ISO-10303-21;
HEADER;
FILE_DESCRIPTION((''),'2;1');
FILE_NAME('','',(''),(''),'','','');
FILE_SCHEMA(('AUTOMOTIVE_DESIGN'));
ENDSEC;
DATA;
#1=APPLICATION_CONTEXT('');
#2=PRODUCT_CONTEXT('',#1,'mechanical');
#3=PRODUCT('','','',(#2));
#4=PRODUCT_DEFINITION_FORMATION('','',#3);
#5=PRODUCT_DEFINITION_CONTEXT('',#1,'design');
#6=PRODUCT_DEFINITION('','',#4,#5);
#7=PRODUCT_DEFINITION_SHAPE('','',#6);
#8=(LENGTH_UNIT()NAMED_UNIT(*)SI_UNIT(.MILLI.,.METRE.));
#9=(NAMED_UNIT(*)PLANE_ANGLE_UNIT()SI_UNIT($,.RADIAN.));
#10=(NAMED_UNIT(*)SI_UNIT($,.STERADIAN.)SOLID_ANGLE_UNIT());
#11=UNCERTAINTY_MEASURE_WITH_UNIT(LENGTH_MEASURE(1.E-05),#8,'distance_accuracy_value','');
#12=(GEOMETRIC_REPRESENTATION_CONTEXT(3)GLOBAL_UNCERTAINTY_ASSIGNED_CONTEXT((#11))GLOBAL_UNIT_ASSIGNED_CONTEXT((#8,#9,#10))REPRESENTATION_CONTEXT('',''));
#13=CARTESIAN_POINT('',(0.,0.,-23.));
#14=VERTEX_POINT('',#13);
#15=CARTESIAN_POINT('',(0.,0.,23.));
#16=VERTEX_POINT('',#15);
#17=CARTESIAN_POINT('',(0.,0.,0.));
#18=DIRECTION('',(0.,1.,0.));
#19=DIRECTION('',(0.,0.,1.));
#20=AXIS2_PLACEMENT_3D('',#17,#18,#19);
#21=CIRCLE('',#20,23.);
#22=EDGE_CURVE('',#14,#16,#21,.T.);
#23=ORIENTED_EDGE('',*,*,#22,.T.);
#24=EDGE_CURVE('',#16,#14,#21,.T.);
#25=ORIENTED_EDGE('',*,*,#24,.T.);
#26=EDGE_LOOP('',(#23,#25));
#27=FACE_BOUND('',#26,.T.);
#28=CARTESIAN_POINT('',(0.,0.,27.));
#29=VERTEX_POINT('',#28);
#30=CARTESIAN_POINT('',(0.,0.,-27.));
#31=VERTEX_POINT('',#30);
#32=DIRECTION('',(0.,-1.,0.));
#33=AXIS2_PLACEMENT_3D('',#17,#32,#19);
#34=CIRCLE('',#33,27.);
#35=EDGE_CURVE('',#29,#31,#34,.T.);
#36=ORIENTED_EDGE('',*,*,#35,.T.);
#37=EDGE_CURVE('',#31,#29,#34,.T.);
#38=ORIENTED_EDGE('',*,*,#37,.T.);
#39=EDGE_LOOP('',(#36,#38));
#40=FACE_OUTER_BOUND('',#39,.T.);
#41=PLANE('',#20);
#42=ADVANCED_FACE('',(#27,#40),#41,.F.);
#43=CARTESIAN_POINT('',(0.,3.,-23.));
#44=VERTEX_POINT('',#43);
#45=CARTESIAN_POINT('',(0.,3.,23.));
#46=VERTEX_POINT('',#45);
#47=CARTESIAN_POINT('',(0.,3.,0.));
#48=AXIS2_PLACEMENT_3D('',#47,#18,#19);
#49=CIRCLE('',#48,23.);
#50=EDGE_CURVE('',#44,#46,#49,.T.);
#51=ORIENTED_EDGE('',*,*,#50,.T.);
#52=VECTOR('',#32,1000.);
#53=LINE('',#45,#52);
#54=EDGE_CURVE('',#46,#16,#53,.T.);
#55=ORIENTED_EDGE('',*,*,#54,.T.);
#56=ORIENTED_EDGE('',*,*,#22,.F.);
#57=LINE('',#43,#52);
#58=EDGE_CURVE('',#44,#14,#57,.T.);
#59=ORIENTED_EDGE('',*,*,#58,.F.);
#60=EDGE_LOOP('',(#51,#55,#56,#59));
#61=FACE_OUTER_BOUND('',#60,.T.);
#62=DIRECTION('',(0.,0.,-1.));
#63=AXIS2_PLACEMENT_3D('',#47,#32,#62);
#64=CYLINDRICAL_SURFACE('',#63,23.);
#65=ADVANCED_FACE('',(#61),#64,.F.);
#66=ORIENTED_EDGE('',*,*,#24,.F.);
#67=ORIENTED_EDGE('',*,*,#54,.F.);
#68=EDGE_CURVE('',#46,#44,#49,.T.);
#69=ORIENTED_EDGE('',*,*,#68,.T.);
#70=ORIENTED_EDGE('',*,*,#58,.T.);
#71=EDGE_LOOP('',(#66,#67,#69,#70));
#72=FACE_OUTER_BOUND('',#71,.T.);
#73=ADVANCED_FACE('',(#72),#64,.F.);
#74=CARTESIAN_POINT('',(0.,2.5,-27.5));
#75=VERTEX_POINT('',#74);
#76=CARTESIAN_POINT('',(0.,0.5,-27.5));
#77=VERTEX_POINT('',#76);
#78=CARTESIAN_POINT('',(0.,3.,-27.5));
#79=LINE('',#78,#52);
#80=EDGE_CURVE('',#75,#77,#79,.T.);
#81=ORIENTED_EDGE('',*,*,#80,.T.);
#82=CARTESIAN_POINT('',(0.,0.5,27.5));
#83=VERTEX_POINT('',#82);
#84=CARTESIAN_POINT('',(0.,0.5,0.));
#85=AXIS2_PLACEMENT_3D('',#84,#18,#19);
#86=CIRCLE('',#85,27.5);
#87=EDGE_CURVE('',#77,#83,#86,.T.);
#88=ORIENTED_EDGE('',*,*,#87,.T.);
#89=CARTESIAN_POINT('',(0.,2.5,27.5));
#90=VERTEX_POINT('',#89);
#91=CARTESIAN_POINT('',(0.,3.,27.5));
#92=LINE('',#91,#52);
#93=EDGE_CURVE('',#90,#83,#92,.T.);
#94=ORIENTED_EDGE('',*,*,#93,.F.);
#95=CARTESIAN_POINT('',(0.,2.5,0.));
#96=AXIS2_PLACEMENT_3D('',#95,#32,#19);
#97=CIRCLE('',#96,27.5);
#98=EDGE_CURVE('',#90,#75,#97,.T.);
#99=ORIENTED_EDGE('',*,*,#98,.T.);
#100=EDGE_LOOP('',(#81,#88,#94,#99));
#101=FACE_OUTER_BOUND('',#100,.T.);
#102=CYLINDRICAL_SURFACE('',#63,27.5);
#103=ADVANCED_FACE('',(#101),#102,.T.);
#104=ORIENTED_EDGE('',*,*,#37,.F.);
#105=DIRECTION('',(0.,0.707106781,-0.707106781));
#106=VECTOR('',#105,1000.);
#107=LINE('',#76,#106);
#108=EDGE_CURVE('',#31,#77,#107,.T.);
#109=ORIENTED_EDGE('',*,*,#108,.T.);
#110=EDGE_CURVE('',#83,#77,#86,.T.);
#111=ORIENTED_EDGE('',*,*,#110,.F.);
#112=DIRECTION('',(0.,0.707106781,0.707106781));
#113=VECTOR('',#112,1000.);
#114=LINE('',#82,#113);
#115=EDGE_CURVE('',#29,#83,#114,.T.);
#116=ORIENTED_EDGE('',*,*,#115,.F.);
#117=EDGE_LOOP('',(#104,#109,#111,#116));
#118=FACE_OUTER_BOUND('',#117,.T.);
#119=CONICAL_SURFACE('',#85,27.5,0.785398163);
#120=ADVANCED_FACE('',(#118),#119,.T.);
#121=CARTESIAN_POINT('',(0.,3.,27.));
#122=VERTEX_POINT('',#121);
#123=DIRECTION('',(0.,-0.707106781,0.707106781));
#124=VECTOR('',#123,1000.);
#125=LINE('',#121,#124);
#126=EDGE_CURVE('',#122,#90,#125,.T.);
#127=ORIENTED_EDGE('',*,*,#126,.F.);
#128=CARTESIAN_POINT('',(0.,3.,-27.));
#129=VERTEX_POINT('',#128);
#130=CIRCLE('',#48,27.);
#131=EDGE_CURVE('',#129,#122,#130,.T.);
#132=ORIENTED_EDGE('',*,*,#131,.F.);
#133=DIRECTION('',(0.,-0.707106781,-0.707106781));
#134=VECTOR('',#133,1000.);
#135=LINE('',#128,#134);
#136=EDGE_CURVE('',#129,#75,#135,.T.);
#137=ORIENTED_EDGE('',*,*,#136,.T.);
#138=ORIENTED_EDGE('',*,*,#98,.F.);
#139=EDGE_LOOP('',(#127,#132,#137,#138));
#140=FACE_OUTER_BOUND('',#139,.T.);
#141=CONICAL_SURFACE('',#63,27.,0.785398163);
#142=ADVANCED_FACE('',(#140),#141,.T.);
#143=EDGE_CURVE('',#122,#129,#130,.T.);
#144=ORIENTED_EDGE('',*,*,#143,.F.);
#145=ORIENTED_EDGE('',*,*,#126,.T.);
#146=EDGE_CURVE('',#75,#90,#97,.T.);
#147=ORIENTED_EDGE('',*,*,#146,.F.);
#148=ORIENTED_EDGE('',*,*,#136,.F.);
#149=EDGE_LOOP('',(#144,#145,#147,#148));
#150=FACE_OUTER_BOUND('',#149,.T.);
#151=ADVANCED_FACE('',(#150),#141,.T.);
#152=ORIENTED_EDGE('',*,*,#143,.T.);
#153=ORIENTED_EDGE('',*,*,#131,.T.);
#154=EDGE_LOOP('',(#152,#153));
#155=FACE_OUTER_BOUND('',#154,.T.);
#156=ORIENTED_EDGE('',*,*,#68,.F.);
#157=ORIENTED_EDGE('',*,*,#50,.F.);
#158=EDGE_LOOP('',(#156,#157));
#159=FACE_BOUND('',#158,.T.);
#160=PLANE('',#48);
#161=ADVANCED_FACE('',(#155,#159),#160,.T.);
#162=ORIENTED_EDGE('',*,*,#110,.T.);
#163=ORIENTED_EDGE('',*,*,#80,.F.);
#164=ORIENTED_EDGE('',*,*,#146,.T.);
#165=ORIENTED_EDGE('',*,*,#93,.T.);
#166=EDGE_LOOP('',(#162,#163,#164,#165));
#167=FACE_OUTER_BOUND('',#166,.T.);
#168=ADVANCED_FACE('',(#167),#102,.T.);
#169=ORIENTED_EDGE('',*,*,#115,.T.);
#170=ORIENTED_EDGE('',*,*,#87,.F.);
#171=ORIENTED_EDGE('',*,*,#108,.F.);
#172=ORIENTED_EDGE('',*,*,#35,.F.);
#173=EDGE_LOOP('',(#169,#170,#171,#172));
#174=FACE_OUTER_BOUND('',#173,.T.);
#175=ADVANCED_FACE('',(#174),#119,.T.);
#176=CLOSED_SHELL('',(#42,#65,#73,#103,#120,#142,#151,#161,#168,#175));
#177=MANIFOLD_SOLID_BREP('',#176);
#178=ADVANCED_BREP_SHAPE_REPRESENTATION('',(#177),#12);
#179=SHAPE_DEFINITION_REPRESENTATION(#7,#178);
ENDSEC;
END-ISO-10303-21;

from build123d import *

# Parameters (mm, degrees)
SKETCH1_R           = 27.5
SKETCH1_R_2         = 23
BOSS_EXTRUDE1_DEPTH = 3
CHAMFER1_SIZE       = 0.5


with BuildPart() as part:
    # Sketch1 → Boss-Extrude1 (new body)
    with BuildSketch(Plane(origin=(0, 0, 0), x_dir=(1, 0, 0), z_dir=(0, 1, 0))):
        with Locations(Location((0, 0, 0), (0, 0, 270))):
            Circle(SKETCH1_R)
        with Locations(Location((0, 0, 0), (0, 0, 270))):
            Circle(SKETCH1_R_2, mode=Mode.SUBTRACT)
    extrude(amount=BOSS_EXTRUDE1_DEPTH)

    # Chamfer1
    chamfer1_edges = [part.edges().sort_by_distance(p)[0] for p in [
        (0, 0, -27.5),
        (0, 3, -27.5),
    ]]
    chamfer(chamfer1_edges, length=CHAMFER1_SIZE)


solid = part.part
